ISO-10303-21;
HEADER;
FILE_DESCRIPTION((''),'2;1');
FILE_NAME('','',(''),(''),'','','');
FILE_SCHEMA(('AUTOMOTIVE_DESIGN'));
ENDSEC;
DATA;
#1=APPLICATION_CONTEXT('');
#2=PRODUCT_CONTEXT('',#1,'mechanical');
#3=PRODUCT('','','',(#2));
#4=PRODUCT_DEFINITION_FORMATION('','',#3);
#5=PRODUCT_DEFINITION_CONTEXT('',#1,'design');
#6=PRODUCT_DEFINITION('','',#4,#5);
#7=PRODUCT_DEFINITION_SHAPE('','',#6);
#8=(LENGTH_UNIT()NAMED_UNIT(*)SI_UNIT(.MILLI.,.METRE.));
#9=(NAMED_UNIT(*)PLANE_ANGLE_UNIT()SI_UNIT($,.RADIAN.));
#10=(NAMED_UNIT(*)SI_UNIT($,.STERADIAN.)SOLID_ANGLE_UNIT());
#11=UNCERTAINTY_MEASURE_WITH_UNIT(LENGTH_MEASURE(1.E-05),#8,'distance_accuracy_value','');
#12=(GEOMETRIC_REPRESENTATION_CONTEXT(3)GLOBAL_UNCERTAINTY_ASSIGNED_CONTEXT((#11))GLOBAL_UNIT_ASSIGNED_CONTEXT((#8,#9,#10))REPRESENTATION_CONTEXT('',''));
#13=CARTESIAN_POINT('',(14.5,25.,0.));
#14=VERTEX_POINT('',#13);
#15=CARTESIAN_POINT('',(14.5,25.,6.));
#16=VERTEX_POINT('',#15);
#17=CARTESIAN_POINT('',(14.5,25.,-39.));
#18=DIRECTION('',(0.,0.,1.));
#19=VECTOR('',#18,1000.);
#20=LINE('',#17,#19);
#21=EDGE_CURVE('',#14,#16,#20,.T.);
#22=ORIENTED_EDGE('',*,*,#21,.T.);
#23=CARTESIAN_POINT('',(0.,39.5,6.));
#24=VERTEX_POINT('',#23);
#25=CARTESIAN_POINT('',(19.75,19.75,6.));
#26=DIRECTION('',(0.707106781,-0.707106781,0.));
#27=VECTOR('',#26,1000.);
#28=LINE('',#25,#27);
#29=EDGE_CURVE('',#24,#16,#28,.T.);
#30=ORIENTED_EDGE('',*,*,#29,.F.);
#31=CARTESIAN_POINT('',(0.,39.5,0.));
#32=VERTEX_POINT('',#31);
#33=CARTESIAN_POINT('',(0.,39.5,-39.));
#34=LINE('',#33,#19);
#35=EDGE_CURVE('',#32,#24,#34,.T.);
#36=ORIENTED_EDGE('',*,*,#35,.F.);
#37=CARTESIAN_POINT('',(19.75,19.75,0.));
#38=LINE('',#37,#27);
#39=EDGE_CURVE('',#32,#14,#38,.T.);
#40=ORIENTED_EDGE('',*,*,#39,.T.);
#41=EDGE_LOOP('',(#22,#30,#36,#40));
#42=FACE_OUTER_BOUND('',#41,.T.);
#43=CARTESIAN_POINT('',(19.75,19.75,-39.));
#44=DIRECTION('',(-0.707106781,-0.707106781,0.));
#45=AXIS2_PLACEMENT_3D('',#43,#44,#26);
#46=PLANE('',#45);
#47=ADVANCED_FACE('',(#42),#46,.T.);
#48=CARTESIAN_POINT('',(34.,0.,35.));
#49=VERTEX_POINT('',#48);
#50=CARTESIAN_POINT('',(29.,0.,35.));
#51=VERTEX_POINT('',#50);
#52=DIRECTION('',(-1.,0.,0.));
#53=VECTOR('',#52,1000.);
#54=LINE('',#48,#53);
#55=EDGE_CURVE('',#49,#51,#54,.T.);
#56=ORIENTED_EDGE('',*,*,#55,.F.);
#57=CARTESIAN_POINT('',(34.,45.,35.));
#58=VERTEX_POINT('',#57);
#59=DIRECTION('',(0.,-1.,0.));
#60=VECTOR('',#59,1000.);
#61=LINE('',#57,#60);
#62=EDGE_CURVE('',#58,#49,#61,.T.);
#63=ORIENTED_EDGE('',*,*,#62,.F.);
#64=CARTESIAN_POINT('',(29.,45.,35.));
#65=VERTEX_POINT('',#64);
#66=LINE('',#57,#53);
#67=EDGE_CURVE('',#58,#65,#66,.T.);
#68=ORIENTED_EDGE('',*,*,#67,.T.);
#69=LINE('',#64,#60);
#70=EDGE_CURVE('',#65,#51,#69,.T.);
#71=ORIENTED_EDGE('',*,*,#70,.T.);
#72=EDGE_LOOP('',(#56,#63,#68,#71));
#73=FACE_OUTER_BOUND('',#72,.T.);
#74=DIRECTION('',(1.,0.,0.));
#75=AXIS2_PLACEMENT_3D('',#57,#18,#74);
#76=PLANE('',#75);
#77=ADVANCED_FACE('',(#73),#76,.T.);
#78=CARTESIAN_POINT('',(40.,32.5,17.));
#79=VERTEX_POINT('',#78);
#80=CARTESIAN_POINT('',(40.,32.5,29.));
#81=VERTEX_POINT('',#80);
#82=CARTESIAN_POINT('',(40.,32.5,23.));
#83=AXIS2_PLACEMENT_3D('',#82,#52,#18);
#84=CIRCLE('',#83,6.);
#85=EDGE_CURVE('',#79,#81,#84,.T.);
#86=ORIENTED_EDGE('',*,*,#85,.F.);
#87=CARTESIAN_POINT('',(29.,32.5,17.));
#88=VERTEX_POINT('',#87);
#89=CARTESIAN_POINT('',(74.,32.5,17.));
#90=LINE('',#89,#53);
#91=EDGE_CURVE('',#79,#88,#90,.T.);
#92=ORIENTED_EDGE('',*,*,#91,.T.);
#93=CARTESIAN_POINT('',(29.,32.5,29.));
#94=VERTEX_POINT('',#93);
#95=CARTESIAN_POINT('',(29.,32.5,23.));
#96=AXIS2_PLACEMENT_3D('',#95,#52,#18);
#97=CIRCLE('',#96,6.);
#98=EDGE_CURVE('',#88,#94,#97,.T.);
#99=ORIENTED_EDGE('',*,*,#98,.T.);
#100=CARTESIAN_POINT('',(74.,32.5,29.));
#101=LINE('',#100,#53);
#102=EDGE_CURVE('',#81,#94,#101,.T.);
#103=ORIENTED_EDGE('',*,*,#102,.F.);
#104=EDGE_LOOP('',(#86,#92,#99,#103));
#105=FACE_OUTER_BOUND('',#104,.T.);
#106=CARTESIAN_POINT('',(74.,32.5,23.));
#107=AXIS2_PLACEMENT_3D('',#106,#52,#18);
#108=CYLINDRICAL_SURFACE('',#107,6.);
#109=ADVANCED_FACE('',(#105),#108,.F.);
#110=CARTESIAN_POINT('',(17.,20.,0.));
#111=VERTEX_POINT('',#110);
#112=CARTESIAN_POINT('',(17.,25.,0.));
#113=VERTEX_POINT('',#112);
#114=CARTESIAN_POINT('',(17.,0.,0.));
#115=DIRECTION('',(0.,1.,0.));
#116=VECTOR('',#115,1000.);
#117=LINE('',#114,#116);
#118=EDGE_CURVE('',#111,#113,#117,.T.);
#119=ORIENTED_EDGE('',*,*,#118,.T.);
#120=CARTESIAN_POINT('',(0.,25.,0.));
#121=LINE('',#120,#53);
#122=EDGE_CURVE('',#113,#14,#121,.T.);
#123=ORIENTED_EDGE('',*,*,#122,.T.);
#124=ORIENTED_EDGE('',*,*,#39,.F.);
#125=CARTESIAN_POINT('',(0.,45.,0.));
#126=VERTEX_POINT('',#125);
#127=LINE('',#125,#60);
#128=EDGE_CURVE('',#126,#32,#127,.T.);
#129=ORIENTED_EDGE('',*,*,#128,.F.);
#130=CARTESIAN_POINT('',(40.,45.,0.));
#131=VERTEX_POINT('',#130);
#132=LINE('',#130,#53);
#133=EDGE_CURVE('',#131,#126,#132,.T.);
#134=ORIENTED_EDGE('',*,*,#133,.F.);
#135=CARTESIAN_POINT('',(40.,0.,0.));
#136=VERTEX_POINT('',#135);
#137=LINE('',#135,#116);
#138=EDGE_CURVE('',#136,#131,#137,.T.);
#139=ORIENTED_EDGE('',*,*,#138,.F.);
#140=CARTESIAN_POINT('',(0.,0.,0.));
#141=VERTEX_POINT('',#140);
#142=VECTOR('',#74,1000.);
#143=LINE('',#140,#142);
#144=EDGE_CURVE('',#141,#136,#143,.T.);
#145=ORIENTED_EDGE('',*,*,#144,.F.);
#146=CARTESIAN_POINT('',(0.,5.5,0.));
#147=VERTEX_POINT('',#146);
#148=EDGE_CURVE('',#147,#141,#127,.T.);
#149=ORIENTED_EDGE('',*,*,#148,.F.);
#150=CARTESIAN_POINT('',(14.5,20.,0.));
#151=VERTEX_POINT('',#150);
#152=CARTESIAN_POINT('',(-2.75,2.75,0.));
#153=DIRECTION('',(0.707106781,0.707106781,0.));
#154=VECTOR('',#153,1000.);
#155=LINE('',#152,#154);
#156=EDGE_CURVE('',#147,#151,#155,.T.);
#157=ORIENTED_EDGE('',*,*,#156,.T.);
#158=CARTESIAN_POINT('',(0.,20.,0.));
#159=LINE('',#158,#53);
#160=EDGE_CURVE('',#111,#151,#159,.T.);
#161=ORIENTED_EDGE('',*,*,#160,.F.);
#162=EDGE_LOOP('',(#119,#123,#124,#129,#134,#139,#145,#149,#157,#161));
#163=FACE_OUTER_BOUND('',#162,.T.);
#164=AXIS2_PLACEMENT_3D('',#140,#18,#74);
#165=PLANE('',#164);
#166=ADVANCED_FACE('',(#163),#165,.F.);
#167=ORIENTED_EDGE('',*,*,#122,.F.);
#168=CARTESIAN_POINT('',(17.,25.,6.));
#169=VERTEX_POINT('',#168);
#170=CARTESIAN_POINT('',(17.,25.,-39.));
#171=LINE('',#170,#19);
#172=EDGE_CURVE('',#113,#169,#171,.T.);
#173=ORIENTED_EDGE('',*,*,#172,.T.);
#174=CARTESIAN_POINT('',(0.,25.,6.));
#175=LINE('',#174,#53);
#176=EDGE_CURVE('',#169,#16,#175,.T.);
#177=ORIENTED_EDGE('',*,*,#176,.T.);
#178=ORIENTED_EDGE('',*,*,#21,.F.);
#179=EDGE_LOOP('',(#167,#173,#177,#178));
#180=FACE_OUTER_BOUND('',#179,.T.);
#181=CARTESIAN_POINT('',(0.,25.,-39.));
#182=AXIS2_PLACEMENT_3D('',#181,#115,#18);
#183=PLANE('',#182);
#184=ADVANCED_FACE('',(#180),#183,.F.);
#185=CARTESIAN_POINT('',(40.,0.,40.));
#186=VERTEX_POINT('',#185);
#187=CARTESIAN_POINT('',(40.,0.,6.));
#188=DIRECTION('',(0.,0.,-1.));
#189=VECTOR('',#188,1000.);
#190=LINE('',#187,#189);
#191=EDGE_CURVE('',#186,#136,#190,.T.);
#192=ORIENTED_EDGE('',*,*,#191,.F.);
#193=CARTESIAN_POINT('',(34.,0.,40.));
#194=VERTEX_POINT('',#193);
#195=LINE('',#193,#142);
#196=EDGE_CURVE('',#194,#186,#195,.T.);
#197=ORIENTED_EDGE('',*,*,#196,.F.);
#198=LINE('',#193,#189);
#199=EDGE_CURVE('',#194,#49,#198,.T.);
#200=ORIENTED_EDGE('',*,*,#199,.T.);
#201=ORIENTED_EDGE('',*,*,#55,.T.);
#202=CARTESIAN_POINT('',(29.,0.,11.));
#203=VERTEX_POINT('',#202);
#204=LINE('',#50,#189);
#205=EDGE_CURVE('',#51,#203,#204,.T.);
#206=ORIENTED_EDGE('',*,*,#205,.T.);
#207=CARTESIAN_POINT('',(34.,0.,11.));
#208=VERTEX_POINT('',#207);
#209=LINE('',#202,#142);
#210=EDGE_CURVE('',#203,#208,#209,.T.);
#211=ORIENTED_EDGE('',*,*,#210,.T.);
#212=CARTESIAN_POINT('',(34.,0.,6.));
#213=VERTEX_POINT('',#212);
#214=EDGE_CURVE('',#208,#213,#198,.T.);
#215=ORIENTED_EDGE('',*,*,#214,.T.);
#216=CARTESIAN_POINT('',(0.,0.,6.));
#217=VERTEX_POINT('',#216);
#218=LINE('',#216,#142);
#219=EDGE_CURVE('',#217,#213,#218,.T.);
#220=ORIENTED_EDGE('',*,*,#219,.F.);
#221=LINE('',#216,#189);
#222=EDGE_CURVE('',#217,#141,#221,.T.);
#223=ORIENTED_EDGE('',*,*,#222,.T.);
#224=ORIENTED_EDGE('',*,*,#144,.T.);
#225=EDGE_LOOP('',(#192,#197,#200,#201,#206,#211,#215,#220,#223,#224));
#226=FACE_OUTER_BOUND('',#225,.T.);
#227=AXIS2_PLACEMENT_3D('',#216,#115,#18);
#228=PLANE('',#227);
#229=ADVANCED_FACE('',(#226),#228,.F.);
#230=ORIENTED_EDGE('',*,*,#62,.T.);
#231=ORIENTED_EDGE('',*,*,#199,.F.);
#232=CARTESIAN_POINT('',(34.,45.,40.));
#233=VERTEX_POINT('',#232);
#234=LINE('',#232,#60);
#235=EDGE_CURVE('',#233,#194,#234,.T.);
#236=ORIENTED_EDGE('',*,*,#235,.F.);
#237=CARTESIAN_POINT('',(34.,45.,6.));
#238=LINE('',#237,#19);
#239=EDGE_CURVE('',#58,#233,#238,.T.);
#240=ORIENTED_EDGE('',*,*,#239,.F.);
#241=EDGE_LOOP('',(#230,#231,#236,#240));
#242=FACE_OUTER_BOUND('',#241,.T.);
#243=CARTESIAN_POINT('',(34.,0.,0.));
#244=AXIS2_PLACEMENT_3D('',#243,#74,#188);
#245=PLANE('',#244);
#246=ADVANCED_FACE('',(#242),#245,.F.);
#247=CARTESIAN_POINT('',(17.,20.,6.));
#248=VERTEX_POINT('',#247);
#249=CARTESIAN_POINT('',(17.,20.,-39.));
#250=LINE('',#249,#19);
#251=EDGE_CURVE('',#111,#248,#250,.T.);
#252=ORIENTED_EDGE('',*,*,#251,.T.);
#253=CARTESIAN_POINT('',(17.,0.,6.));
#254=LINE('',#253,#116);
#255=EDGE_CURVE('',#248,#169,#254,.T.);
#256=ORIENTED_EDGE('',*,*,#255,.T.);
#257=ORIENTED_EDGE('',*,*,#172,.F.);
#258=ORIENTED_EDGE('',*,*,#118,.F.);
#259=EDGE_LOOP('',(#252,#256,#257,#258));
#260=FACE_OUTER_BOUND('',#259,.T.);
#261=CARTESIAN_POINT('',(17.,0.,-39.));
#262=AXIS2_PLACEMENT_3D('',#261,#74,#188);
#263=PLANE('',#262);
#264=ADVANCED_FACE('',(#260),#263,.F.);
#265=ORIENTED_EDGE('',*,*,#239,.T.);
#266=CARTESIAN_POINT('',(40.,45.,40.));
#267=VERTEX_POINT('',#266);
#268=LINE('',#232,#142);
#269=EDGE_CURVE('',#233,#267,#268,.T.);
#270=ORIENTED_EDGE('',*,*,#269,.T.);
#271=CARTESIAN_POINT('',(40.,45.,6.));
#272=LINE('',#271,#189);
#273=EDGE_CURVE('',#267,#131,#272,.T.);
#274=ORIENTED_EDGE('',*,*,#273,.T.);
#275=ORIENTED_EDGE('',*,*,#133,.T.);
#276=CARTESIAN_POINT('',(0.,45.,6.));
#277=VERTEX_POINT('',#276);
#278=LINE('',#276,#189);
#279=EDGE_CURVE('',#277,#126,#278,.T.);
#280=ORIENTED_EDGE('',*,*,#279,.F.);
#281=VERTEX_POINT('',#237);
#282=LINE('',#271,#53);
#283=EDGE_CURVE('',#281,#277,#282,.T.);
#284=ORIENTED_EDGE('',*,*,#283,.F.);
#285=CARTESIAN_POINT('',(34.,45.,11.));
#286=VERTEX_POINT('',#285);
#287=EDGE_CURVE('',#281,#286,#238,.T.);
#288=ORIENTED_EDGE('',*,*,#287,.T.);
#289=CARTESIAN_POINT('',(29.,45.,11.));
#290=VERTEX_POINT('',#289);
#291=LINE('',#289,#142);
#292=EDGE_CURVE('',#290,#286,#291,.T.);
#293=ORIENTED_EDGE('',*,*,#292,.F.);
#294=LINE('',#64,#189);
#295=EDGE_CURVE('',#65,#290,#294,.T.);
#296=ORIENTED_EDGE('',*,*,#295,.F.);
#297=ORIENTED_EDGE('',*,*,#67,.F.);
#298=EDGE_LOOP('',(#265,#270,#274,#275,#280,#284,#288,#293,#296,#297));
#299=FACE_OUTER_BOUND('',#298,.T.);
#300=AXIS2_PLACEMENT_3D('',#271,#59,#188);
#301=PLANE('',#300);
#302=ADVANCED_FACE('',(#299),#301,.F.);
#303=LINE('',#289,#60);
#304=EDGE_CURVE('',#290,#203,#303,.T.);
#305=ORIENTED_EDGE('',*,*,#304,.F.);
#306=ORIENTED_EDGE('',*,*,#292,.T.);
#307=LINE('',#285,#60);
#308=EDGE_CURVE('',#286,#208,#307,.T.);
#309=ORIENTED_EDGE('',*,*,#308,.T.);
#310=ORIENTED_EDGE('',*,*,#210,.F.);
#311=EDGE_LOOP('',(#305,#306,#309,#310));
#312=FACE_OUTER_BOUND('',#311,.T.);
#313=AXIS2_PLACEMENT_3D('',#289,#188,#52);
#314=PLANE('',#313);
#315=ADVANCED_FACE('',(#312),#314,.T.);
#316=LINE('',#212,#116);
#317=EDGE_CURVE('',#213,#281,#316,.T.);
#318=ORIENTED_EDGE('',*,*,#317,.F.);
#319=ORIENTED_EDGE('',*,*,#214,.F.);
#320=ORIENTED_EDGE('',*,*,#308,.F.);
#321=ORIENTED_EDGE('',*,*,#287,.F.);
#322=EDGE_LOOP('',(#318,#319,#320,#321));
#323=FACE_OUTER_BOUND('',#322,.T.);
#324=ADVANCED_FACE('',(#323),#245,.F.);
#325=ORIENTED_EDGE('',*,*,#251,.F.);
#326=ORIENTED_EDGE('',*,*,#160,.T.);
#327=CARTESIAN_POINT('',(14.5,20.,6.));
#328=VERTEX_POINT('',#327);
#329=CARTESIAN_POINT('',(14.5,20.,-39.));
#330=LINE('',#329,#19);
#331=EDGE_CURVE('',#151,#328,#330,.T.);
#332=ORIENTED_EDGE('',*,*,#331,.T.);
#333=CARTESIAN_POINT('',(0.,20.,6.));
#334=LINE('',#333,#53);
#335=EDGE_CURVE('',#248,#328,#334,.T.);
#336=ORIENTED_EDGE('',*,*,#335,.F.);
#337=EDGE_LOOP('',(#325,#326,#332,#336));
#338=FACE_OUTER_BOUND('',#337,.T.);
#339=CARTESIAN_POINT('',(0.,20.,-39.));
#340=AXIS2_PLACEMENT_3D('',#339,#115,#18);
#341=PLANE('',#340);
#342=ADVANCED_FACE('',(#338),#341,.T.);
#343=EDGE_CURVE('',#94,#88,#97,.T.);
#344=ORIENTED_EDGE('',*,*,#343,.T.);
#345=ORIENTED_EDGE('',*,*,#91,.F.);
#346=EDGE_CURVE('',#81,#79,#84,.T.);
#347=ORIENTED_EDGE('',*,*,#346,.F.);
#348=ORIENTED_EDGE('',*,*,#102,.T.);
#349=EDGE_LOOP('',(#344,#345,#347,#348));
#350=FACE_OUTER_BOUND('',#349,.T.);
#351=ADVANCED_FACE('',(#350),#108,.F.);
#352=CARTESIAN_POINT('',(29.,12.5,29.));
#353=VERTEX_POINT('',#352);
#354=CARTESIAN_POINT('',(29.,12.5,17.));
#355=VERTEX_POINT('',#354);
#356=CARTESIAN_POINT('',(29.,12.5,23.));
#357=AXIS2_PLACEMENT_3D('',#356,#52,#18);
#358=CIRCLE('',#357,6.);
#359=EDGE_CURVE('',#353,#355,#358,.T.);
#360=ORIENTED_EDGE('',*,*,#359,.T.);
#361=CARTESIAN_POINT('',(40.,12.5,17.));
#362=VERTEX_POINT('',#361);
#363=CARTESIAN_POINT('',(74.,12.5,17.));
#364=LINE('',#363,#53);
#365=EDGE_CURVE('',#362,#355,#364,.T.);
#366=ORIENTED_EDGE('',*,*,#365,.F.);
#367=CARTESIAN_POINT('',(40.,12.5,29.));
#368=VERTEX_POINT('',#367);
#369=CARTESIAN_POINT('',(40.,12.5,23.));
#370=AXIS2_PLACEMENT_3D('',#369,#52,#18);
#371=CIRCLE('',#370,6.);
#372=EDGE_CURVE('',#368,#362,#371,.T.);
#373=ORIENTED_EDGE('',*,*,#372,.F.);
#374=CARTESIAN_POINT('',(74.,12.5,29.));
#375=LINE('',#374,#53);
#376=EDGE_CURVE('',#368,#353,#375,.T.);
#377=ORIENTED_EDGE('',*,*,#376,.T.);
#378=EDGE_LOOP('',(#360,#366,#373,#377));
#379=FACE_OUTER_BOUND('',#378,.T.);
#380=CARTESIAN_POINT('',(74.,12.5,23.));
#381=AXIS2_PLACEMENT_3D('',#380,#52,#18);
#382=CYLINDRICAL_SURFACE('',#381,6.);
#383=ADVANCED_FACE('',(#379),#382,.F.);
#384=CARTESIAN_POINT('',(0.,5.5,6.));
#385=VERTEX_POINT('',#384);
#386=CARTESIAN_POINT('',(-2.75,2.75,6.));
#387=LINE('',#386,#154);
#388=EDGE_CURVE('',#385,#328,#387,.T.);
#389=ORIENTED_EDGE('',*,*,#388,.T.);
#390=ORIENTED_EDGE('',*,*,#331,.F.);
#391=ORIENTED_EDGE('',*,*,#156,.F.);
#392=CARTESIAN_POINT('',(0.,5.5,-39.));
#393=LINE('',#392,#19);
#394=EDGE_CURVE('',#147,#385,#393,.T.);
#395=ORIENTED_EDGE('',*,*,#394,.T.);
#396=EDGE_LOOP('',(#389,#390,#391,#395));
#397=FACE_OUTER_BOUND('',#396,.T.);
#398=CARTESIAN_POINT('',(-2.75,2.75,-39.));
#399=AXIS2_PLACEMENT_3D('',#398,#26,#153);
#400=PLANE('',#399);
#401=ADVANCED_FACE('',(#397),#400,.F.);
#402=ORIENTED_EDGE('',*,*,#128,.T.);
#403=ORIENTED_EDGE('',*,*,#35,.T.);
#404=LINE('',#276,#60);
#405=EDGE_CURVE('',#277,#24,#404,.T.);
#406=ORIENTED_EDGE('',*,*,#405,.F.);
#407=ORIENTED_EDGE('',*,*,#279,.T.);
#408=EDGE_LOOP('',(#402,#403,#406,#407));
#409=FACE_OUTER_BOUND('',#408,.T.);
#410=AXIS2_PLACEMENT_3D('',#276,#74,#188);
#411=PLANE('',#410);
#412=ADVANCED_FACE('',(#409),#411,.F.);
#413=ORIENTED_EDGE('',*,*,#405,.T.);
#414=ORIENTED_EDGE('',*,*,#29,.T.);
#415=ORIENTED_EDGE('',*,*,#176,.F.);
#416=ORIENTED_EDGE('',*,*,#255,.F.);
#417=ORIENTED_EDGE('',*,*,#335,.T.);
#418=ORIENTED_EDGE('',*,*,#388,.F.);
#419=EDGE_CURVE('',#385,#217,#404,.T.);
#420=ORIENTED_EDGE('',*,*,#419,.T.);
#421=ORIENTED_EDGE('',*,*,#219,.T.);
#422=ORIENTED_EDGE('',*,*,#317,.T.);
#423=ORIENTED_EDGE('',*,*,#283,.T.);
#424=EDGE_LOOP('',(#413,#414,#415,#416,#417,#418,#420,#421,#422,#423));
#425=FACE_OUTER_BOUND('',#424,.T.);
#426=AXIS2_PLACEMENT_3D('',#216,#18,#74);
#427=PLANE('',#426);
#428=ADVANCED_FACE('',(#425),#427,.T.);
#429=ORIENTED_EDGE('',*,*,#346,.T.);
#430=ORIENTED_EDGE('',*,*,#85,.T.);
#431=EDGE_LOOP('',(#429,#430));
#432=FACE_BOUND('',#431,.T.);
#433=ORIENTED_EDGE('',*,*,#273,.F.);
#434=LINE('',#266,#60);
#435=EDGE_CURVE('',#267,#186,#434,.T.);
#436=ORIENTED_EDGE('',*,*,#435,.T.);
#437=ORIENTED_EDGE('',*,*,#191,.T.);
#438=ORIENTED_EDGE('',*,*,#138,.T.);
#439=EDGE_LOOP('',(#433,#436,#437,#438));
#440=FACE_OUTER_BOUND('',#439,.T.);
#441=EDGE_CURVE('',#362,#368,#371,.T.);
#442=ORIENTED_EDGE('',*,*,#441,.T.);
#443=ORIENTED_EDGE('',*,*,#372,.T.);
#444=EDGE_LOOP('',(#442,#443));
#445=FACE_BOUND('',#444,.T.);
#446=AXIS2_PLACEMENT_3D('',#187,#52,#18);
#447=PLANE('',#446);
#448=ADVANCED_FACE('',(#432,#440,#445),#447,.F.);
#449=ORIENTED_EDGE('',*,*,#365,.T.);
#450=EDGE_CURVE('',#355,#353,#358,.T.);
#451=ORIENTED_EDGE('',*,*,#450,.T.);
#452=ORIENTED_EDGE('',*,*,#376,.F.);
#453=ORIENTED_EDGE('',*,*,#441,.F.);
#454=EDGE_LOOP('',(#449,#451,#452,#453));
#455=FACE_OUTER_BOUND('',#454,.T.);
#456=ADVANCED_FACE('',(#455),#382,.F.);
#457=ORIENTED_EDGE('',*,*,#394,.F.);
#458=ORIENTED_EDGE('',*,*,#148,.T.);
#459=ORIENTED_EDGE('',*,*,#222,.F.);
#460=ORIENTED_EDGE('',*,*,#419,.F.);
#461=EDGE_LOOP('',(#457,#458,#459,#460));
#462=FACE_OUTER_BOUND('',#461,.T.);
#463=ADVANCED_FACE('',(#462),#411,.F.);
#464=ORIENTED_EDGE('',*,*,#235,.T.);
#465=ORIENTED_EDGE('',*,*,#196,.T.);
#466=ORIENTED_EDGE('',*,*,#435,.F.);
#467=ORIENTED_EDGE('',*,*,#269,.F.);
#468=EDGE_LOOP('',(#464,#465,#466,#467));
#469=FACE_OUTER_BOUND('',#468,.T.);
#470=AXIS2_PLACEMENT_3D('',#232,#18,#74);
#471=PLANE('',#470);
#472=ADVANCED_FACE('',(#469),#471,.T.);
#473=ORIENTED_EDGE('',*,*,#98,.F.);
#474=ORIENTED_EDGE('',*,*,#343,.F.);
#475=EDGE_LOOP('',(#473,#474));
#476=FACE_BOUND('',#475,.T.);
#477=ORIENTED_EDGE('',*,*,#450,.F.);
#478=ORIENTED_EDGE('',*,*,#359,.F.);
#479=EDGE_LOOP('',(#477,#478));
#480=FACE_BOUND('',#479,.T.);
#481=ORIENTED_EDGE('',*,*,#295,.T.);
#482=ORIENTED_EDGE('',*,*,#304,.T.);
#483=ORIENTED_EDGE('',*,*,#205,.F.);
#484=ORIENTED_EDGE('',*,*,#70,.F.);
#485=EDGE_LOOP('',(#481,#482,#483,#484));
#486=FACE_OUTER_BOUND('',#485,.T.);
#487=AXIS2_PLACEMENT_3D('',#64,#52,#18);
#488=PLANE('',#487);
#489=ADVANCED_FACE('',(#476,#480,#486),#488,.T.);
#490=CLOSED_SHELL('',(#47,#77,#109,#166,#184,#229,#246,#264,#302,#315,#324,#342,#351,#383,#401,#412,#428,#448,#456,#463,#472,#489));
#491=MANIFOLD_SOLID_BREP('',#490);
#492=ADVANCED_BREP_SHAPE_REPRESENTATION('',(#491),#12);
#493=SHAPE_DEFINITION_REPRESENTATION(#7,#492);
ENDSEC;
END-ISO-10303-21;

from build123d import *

# Parameters (mm, degrees)
BASE_PLATE_SKETCH_W        = 40
BASE_PLATE_SKETCH_H        = 45
BASE_PLATE_DEPTH           = 6
UPRIGHT_FLANGE_SKETCH_W    = 34
UPRIGHT_FLANGE_SKETCH_H    = 45
UPRIGHT_FLANGE_DEPTH       = 6
SUPPORT_WEB_SKETCH_W       = 5
SUPPORT_WEB_SKETCH_H       = 24
SUPPORT_WEB_DEPTH          = 45
CORNER_RELIEF_GROOVE_DEPTH = 45
MOUNTING_HOLES_SKETCH_R    = 6
MOUNTING_HOLES_2X_DEPTH    = 45


with BuildPart() as part:
    # Base Plate Sketch → Base Plate (new body)
    with BuildSketch(Plane.XY):
        with Locations((20, 22.5)):
            Rectangle(BASE_PLATE_SKETCH_W, BASE_PLATE_SKETCH_H)
    extrude(amount=BASE_PLATE_DEPTH)

    # Upright Flange Sketch → Upright Flange (add)
    with BuildSketch(Plane(origin=(40, 0, 0), x_dir=(0, 0, -1), z_dir=(1, 0, 0))):
        with Locations((-23, 22.5)):
            Rectangle(UPRIGHT_FLANGE_SKETCH_W, UPRIGHT_FLANGE_SKETCH_H)
    extrude(amount=-UPRIGHT_FLANGE_DEPTH)

    # Support Web Sketch → Support Web (add)
    with BuildSketch(Plane.XZ):
        with Locations((31.5, 23)):
            Rectangle(SUPPORT_WEB_SKETCH_W, SUPPORT_WEB_SKETCH_H)
    extrude(amount=-SUPPORT_WEB_DEPTH)

    # Corner Relief Groove Sketch → Corner Relief Groove (cut)
    with BuildSketch(Plane.XY.offset(6)):
        Polygon((0, 39.5), (0, 22.5), (17, 22.5), (17, 25), (14.5, 25), align=None)
        Polygon((17, 22.5), (0, 22.5), (0, 5.5), (14.5, 20), (17, 20), align=None)
    extrude(amount=-CORNER_RELIEF_GROOVE_DEPTH, mode=Mode.SUBTRACT)

    # Mounting Holes Sketch → Mounting Holes 2x (cut)
    with BuildSketch(Plane.ZY.offset(-29)):
        with Locations((23, 32.5)):
            Circle(MOUNTING_HOLES_SKETCH_R)
        with Locations((23, 12.5)):
            Circle(MOUNTING_HOLES_SKETCH_R)
    extrude(amount=-MOUNTING_HOLES_2X_DEPTH, mode=Mode.SUBTRACT)


solid = part.part
